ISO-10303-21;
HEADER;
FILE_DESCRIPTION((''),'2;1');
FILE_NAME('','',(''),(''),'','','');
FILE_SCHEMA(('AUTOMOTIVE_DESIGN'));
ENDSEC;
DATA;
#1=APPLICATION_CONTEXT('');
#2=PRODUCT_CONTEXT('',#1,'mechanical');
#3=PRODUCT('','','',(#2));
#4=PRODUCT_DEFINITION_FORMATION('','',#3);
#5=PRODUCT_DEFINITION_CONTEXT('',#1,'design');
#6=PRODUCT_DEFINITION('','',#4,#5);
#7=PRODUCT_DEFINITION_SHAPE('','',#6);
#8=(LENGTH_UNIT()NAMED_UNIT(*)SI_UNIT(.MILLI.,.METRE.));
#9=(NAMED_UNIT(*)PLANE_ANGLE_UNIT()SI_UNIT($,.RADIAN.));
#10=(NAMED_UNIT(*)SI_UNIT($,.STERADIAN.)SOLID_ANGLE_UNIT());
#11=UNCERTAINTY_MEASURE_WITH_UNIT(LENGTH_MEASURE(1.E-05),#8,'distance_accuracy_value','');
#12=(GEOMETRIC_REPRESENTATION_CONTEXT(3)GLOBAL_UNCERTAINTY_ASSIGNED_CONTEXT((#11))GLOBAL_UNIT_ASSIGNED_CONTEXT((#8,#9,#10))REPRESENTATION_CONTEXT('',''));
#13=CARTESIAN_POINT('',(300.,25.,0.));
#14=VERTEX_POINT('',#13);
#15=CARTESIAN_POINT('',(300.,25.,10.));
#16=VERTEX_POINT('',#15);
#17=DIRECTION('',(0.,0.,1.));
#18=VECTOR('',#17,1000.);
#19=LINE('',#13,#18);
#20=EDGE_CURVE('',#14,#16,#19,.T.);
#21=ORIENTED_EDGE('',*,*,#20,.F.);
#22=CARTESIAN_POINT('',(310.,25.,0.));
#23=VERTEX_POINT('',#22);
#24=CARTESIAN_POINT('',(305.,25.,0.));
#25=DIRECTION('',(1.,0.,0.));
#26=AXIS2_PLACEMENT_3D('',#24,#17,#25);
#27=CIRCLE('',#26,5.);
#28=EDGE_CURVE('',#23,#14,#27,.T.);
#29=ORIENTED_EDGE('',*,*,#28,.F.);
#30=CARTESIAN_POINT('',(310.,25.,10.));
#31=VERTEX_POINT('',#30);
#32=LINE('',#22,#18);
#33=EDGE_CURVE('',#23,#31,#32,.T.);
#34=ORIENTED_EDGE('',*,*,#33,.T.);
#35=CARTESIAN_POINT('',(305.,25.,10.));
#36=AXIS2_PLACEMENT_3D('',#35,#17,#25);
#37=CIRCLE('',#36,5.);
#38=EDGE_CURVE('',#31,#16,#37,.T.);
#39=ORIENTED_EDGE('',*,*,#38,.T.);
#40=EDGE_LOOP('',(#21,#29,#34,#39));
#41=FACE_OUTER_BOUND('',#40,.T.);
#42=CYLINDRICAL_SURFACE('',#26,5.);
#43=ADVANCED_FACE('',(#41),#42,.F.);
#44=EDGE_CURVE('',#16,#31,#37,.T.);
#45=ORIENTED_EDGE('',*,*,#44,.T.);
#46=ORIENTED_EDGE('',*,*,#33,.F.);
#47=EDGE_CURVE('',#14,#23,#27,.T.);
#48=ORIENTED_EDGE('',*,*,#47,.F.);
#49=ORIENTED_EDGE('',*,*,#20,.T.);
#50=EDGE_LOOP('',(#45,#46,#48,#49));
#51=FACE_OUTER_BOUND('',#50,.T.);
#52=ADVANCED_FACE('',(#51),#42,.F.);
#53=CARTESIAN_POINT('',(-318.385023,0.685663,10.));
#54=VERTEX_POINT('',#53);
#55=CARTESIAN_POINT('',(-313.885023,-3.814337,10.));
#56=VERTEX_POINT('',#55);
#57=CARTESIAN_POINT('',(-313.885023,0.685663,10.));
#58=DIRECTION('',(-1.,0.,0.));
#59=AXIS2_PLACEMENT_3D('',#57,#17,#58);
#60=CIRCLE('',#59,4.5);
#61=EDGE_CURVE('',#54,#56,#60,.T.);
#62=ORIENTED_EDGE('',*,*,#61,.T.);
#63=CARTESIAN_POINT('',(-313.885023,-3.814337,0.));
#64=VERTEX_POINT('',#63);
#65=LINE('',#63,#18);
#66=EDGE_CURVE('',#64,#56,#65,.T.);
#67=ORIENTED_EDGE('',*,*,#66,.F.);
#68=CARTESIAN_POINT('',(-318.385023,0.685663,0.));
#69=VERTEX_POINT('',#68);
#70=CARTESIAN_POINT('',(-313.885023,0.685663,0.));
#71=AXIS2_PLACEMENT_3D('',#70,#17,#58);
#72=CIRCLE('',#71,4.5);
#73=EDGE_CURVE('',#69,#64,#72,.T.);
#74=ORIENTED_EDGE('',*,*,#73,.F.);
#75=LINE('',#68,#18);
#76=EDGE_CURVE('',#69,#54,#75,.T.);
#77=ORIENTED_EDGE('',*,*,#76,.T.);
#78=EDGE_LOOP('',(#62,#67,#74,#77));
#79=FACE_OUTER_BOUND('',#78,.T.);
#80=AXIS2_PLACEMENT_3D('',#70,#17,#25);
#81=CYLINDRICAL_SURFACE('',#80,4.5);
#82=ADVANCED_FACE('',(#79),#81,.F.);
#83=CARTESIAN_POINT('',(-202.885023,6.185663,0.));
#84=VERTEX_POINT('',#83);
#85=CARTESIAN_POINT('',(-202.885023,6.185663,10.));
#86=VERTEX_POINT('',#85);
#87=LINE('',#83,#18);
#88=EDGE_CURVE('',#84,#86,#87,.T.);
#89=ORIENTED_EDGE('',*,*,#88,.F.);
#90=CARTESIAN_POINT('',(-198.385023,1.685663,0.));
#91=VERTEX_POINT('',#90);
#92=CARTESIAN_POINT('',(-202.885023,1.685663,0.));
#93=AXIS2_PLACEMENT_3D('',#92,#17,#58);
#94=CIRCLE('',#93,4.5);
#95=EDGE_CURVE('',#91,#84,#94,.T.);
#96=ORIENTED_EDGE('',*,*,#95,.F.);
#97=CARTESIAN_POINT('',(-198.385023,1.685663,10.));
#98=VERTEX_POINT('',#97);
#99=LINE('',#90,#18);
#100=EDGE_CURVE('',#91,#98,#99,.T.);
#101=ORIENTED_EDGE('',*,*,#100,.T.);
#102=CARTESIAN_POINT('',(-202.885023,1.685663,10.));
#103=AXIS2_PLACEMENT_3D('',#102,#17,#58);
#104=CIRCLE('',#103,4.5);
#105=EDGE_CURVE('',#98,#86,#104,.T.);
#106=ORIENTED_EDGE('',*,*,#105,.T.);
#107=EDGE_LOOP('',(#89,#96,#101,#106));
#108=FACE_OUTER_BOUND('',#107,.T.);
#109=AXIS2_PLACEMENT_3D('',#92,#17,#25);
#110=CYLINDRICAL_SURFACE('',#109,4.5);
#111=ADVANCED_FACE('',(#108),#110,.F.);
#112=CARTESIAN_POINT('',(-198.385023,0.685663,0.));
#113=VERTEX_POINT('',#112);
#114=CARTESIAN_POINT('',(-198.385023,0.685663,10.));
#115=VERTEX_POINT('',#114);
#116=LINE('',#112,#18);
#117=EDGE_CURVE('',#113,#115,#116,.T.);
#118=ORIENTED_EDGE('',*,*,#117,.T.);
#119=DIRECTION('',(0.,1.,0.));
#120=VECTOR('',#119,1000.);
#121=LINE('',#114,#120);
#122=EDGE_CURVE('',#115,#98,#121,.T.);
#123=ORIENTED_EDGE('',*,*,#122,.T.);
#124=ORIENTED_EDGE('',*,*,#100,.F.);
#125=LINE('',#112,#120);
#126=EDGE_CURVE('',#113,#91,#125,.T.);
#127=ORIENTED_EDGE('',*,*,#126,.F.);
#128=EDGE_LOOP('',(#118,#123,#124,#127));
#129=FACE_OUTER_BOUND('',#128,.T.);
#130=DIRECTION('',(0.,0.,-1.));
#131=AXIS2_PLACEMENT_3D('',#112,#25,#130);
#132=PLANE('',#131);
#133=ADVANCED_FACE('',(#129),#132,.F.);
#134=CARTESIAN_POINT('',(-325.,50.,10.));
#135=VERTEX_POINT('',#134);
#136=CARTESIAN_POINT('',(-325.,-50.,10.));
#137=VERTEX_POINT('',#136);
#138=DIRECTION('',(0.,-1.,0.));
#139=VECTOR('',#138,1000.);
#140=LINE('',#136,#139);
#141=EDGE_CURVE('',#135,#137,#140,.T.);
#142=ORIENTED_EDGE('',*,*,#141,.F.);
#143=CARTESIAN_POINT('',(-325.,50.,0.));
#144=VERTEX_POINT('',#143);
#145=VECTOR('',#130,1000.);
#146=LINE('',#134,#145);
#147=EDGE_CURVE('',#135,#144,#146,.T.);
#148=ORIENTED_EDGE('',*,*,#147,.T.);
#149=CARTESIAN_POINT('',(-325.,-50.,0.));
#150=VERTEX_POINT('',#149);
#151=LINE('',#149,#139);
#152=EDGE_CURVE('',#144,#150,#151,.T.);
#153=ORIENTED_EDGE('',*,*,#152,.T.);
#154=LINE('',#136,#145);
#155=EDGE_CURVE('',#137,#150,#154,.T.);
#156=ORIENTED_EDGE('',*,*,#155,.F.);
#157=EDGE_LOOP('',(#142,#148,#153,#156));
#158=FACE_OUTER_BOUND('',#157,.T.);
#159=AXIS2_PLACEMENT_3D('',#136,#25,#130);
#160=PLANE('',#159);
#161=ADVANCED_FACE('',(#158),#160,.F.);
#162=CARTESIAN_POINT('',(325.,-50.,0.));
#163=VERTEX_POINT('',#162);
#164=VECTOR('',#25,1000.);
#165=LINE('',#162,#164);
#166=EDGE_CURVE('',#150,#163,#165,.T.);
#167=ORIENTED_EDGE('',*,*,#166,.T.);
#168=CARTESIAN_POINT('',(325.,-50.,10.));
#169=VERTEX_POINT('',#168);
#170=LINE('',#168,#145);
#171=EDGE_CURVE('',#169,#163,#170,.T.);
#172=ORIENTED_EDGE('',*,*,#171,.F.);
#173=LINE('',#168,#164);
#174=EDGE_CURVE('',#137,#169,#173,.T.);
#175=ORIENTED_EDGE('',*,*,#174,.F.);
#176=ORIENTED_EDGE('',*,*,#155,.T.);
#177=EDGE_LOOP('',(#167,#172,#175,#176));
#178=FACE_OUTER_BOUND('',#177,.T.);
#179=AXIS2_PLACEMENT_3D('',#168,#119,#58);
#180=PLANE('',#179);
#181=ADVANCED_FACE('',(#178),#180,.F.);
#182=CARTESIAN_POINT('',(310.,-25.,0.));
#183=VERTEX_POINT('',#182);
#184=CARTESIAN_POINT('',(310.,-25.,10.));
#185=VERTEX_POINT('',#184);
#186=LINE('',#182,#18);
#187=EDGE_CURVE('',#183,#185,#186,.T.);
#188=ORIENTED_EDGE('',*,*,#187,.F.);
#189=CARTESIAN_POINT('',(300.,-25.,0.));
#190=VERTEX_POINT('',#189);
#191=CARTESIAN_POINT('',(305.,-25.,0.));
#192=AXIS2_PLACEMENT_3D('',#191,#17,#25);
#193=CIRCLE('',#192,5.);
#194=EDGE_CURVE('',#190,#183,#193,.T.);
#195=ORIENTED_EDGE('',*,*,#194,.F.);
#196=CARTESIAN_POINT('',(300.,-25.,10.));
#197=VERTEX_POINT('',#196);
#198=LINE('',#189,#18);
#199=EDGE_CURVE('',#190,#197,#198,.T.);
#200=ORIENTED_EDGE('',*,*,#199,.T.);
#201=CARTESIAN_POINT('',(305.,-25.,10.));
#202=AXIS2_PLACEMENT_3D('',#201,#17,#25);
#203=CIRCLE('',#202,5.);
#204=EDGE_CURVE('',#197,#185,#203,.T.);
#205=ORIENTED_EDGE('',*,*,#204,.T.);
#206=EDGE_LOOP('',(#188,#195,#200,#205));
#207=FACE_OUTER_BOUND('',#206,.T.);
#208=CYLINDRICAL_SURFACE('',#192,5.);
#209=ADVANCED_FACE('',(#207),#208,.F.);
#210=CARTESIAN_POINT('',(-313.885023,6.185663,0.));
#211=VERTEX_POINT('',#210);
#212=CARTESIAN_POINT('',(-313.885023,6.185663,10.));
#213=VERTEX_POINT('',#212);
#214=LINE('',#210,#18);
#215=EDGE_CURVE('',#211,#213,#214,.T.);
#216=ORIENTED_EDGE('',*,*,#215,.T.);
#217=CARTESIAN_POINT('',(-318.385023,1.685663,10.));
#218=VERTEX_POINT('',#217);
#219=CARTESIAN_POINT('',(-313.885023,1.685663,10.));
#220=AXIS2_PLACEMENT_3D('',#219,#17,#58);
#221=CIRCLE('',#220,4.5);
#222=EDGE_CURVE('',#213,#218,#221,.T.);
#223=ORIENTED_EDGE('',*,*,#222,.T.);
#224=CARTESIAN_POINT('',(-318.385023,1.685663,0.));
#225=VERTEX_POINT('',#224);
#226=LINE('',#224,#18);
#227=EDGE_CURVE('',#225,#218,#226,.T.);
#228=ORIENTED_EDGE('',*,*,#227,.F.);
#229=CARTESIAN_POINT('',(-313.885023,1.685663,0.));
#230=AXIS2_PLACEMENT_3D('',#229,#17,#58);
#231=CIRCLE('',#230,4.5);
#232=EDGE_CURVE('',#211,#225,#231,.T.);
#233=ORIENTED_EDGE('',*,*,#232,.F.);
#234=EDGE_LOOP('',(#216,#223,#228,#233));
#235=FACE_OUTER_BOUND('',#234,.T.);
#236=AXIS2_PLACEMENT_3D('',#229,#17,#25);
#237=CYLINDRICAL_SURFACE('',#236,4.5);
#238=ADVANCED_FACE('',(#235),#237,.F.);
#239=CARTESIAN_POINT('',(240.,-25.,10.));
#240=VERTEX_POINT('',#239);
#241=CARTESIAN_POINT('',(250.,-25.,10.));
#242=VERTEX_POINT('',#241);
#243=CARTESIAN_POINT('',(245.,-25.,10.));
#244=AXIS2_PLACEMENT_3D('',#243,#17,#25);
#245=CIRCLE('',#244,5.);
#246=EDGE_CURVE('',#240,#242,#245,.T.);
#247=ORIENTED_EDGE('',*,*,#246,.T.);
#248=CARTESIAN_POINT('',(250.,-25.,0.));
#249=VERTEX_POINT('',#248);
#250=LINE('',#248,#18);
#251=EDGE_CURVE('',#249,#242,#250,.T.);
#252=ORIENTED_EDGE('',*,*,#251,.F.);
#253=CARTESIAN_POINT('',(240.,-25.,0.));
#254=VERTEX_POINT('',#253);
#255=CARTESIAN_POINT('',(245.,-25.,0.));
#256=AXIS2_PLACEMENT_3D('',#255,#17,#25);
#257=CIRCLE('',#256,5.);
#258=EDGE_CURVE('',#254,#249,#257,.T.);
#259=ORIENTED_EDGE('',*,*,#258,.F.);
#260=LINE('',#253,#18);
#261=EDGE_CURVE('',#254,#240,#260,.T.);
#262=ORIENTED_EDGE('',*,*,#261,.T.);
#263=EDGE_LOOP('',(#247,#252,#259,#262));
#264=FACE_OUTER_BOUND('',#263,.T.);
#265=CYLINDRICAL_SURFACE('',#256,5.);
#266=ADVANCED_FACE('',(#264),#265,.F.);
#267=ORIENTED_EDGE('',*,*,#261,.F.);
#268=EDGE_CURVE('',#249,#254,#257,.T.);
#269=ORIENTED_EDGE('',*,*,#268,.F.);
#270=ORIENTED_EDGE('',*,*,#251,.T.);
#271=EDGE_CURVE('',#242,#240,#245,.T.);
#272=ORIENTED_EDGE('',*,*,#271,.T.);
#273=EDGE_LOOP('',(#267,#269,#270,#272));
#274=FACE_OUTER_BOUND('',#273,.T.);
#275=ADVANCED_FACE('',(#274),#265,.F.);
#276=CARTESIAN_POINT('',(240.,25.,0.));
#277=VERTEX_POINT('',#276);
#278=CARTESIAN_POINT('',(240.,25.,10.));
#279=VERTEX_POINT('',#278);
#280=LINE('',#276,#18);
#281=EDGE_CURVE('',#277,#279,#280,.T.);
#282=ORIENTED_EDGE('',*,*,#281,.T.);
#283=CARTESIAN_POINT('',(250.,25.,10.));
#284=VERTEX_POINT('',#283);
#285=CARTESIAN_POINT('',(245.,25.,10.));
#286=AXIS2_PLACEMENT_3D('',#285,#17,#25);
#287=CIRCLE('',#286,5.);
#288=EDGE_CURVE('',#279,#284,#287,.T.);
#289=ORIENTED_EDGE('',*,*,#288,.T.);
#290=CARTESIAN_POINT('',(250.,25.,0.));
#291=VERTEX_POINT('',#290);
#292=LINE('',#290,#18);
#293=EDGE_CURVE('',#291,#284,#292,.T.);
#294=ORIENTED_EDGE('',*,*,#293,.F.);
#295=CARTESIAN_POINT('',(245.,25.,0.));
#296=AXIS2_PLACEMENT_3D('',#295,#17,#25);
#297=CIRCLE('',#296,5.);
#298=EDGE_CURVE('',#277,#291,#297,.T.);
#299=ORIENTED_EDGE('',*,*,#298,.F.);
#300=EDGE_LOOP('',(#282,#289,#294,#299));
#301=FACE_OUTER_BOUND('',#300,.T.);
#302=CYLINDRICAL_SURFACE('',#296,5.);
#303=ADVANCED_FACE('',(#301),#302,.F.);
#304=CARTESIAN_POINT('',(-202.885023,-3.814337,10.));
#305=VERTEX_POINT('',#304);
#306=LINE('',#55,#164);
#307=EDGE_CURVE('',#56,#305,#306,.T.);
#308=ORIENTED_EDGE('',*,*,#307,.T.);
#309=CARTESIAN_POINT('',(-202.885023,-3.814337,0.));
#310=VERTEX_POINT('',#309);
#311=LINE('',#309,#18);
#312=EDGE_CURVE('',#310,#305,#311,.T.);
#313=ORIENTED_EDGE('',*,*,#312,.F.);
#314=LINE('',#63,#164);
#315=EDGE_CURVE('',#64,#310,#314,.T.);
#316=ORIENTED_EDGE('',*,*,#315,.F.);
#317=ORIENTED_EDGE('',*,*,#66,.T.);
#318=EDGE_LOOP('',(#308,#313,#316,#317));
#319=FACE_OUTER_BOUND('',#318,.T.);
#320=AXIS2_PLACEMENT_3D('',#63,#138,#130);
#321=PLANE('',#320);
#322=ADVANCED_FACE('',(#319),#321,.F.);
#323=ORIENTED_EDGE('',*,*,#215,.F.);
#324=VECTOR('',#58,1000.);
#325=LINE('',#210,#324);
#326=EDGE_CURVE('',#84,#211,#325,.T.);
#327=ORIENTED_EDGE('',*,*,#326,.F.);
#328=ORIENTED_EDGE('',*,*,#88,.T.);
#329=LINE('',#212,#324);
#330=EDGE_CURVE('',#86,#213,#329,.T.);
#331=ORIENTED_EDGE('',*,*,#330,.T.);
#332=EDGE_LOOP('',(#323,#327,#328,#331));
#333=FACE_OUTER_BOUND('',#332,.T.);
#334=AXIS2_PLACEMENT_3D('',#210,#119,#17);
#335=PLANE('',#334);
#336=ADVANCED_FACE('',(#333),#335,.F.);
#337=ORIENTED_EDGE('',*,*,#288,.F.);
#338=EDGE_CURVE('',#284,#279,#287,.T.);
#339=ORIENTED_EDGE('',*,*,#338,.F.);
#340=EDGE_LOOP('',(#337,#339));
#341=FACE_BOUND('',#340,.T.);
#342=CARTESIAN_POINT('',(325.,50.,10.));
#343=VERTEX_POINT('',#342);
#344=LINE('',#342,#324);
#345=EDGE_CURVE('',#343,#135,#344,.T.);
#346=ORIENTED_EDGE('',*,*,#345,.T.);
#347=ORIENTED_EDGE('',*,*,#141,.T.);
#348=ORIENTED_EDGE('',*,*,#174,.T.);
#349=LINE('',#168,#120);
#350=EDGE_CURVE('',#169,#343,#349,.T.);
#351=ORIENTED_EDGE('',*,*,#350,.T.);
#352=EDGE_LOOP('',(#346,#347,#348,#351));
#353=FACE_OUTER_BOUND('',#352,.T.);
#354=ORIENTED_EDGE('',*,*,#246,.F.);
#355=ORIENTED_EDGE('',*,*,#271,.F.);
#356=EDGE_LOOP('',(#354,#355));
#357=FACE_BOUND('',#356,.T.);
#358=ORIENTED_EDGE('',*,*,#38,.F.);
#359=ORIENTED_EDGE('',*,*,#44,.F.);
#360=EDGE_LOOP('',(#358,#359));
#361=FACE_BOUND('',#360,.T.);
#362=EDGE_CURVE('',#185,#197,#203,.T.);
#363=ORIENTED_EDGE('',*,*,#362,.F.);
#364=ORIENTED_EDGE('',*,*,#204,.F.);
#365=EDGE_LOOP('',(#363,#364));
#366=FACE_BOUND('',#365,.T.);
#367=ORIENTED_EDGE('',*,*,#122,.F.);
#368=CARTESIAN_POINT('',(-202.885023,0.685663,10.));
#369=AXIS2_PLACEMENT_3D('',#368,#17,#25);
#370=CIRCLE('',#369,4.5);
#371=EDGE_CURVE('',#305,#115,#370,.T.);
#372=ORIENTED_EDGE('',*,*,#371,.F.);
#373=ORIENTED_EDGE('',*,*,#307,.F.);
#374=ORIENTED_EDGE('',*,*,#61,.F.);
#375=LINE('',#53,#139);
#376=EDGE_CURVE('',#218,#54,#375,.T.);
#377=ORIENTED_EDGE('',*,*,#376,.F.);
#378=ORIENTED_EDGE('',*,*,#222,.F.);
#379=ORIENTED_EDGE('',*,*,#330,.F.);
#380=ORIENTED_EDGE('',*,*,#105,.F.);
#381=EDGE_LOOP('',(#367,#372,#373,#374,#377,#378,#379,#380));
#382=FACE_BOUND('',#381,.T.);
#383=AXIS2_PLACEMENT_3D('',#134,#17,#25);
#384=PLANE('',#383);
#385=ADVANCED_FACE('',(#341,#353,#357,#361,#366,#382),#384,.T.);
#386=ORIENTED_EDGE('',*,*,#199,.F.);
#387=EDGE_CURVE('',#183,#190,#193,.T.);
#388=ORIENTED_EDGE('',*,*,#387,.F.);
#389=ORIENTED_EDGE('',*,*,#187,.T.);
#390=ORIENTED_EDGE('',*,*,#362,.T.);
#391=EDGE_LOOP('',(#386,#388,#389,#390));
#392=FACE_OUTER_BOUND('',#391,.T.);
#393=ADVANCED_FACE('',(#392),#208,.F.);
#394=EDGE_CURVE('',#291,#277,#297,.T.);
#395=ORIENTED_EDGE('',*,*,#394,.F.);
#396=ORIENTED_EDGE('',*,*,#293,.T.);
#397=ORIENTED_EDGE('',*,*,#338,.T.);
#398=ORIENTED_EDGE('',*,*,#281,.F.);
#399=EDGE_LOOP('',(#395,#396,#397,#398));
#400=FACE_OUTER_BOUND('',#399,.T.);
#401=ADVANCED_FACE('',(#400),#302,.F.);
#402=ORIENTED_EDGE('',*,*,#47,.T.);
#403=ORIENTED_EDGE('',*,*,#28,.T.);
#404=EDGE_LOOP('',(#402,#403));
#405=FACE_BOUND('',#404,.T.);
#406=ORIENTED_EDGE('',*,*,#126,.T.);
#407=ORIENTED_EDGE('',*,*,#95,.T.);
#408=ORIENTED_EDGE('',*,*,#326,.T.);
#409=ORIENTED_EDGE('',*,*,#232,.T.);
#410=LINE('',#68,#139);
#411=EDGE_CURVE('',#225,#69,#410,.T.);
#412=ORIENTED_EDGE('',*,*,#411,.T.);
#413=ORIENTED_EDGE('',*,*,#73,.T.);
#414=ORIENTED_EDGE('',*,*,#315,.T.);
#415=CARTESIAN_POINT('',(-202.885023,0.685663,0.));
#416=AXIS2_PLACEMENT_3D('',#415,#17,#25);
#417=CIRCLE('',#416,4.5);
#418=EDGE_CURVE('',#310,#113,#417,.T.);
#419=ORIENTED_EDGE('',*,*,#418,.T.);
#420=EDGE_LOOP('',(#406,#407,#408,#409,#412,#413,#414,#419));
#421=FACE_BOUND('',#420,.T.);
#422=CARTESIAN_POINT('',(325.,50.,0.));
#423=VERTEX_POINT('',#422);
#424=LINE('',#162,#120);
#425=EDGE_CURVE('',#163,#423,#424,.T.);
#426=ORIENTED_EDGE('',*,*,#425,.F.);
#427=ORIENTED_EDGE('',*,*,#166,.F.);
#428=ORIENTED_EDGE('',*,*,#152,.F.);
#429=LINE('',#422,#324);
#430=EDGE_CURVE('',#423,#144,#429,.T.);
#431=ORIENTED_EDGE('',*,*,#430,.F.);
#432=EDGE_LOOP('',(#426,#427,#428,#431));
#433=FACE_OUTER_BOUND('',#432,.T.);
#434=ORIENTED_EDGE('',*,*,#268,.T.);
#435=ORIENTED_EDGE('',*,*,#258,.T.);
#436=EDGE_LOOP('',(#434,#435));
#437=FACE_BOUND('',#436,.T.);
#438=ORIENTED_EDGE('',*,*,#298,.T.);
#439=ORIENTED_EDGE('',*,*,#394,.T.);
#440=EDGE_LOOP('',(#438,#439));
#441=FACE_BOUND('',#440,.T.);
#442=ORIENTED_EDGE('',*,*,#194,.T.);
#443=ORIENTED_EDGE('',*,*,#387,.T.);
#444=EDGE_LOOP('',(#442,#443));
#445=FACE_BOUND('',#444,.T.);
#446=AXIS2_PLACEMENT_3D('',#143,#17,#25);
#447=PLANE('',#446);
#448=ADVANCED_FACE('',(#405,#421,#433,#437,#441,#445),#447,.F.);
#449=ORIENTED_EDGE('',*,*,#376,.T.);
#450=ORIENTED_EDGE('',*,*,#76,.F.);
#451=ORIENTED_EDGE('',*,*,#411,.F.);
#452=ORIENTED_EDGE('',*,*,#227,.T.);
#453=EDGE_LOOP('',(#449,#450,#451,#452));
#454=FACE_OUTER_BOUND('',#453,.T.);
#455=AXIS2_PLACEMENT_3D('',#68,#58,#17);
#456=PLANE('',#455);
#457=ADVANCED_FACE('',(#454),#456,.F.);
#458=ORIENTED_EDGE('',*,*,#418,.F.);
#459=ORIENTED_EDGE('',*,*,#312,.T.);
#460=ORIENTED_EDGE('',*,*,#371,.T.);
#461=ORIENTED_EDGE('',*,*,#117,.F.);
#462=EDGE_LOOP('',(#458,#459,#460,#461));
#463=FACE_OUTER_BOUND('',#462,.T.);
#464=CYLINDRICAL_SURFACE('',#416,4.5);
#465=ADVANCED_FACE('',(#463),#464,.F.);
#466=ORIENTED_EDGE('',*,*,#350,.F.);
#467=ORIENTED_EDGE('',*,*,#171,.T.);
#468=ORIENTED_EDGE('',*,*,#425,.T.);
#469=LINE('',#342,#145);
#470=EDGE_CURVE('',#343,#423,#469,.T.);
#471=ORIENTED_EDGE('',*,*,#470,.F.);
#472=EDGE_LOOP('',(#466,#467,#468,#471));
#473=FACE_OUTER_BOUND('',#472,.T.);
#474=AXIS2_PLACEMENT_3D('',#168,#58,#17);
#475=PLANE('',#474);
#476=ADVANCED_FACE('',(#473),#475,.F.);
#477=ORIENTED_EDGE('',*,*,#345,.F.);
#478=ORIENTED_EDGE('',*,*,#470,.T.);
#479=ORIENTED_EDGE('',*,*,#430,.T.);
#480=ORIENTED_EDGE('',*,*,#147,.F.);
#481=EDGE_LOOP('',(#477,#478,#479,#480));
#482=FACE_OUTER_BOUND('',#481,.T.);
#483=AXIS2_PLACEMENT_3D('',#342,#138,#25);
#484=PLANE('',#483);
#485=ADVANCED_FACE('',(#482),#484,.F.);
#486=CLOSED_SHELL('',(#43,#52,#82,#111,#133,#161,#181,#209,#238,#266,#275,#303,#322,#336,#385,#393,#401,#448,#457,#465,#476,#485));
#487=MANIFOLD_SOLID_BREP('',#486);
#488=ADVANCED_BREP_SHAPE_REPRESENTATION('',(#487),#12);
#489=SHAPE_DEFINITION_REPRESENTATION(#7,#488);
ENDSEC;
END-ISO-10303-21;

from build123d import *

# Parameters (mm, degrees)
SKETCH1_W           = 650
SKETCH1_H           = 100
BOSS_EXTRUDE1_DEPTH = 10
SKETCH2_R           = 5
CUT_EXTRUDE2_DEPTH  = 10
CUT_EXTRUDE3_DEPTH  = 10


with BuildPart() as part:
    # Sketch1 → Boss-Extrude1 (new body)
    with BuildSketch(Plane.XY):
        Rectangle(SKETCH1_W, SKETCH1_H)
    extrude(amount=BOSS_EXTRUDE1_DEPTH)

    # Sketch2 → Cut-Extrude2 (cut)
    with BuildSketch(Plane.XY.offset(10)):
        with Locations((305, 25)):
            Circle(SKETCH2_R)
        with Locations((245, 25)):
            Circle(SKETCH2_R)
        with Locations((245, -25)):
            Circle(SKETCH2_R)
        with Locations((305, -25)):
            Circle(SKETCH2_R)
    extrude(amount=-CUT_EXTRUDE2_DEPTH, mode=Mode.SUBTRACT)

    # Sketch3 → Cut-Extrude3 (cut)
    with BuildSketch(Plane.XY.offset(10)):
        with BuildLine():
            Line((-313.885022578, -3.814336714), (-202.885022578, -3.814336714))
            ThreePointArc((-202.885022578, -3.814336714), (-199.703042062, -2.496317229), (-198.385022578, 0.685663286))
            Line((-198.385022578, 0.685663286), (-198.385022578, 1.685663286))
            ThreePointArc((-198.385022578, 1.685663286), (-199.703042062, 4.867643802), (-202.885022578, 6.185663286))
            Line((-202.885022578, 6.185663286), (-313.885022578, 6.185663286))
            ThreePointArc((-313.885022578, 6.185663286), (-317.067003093, 4.867643802), (-318.385022578, 1.685663286))
            Line((-318.385022578, 1.685663286), (-318.385022578, 0.685663286))
            ThreePointArc((-318.385022578, 0.685663286), (-317.067003093, -2.496317229), (-313.885022578, -3.814336714))
        make_face()
    extrude(amount=-CUT_EXTRUDE3_DEPTH, mode=Mode.SUBTRACT)


solid = part.part
